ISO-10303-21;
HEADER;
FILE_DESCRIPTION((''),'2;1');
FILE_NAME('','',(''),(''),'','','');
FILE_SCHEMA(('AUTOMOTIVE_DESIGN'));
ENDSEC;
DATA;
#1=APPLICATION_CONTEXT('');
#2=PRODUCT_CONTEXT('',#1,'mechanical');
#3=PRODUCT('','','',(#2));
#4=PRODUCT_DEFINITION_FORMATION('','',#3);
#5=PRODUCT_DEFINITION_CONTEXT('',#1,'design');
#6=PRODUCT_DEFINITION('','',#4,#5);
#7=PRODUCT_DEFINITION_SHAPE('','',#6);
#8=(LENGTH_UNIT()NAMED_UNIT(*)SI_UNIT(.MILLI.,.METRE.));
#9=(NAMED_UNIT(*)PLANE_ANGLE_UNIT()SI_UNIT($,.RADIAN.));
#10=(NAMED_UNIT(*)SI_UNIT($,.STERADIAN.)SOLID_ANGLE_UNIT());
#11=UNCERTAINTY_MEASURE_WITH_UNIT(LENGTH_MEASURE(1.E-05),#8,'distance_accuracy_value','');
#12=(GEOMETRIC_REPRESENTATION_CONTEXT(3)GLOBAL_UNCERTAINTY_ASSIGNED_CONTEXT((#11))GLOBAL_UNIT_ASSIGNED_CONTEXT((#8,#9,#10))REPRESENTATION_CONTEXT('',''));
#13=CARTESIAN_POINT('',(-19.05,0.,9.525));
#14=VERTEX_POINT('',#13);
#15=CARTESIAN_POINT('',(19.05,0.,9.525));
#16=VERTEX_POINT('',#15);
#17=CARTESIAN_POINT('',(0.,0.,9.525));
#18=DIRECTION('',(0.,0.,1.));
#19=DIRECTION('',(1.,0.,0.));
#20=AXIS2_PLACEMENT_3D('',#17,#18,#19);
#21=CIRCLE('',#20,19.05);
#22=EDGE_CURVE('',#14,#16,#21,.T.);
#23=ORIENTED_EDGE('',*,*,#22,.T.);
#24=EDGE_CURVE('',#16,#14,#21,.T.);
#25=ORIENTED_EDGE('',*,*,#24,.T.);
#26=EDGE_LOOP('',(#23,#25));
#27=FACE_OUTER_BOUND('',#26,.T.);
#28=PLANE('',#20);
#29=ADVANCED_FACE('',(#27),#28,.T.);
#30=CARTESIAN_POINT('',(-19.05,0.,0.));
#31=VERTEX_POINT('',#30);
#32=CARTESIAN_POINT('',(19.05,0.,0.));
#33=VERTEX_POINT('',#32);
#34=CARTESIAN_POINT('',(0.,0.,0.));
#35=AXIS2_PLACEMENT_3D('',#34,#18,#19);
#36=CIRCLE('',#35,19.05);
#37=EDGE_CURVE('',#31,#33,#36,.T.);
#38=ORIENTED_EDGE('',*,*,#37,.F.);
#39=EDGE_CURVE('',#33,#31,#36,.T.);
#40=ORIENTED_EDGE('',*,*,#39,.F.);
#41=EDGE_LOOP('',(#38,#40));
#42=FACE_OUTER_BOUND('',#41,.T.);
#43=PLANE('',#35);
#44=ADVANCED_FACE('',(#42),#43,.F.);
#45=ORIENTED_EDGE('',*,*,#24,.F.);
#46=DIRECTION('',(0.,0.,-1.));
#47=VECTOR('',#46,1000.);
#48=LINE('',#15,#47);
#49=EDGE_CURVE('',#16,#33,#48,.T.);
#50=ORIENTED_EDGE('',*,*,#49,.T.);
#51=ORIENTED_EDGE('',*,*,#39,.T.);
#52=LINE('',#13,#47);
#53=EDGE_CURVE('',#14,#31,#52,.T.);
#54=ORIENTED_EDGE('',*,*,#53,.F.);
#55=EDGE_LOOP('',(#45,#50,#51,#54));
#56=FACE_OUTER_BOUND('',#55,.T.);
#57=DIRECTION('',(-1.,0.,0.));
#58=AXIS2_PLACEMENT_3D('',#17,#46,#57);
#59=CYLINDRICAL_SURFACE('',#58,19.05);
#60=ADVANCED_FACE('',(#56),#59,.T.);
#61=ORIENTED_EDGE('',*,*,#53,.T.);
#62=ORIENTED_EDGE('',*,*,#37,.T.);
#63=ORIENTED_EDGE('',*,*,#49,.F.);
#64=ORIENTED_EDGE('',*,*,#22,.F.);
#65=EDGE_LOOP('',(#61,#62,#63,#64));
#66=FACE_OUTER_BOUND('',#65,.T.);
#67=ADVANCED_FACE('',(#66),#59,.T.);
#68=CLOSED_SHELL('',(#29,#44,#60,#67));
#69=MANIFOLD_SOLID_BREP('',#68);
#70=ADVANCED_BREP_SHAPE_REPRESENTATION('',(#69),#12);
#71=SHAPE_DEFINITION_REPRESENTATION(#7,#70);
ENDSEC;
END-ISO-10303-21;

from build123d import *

# Parameters (mm, degrees)
SKETCH1_R           = 19.05
BOSS_EXTRUDE1_DEPTH = 9.525


with BuildPart() as part:
    # Sketch1 → Boss-Extrude1 (new body)
    with BuildSketch(Plane.XY):
        with Locations(Location((0, 0, 0), (0, 0, 180))):
            Circle(SKETCH1_R)
    extrude(amount=BOSS_EXTRUDE1_DEPTH)


solid = part.part
